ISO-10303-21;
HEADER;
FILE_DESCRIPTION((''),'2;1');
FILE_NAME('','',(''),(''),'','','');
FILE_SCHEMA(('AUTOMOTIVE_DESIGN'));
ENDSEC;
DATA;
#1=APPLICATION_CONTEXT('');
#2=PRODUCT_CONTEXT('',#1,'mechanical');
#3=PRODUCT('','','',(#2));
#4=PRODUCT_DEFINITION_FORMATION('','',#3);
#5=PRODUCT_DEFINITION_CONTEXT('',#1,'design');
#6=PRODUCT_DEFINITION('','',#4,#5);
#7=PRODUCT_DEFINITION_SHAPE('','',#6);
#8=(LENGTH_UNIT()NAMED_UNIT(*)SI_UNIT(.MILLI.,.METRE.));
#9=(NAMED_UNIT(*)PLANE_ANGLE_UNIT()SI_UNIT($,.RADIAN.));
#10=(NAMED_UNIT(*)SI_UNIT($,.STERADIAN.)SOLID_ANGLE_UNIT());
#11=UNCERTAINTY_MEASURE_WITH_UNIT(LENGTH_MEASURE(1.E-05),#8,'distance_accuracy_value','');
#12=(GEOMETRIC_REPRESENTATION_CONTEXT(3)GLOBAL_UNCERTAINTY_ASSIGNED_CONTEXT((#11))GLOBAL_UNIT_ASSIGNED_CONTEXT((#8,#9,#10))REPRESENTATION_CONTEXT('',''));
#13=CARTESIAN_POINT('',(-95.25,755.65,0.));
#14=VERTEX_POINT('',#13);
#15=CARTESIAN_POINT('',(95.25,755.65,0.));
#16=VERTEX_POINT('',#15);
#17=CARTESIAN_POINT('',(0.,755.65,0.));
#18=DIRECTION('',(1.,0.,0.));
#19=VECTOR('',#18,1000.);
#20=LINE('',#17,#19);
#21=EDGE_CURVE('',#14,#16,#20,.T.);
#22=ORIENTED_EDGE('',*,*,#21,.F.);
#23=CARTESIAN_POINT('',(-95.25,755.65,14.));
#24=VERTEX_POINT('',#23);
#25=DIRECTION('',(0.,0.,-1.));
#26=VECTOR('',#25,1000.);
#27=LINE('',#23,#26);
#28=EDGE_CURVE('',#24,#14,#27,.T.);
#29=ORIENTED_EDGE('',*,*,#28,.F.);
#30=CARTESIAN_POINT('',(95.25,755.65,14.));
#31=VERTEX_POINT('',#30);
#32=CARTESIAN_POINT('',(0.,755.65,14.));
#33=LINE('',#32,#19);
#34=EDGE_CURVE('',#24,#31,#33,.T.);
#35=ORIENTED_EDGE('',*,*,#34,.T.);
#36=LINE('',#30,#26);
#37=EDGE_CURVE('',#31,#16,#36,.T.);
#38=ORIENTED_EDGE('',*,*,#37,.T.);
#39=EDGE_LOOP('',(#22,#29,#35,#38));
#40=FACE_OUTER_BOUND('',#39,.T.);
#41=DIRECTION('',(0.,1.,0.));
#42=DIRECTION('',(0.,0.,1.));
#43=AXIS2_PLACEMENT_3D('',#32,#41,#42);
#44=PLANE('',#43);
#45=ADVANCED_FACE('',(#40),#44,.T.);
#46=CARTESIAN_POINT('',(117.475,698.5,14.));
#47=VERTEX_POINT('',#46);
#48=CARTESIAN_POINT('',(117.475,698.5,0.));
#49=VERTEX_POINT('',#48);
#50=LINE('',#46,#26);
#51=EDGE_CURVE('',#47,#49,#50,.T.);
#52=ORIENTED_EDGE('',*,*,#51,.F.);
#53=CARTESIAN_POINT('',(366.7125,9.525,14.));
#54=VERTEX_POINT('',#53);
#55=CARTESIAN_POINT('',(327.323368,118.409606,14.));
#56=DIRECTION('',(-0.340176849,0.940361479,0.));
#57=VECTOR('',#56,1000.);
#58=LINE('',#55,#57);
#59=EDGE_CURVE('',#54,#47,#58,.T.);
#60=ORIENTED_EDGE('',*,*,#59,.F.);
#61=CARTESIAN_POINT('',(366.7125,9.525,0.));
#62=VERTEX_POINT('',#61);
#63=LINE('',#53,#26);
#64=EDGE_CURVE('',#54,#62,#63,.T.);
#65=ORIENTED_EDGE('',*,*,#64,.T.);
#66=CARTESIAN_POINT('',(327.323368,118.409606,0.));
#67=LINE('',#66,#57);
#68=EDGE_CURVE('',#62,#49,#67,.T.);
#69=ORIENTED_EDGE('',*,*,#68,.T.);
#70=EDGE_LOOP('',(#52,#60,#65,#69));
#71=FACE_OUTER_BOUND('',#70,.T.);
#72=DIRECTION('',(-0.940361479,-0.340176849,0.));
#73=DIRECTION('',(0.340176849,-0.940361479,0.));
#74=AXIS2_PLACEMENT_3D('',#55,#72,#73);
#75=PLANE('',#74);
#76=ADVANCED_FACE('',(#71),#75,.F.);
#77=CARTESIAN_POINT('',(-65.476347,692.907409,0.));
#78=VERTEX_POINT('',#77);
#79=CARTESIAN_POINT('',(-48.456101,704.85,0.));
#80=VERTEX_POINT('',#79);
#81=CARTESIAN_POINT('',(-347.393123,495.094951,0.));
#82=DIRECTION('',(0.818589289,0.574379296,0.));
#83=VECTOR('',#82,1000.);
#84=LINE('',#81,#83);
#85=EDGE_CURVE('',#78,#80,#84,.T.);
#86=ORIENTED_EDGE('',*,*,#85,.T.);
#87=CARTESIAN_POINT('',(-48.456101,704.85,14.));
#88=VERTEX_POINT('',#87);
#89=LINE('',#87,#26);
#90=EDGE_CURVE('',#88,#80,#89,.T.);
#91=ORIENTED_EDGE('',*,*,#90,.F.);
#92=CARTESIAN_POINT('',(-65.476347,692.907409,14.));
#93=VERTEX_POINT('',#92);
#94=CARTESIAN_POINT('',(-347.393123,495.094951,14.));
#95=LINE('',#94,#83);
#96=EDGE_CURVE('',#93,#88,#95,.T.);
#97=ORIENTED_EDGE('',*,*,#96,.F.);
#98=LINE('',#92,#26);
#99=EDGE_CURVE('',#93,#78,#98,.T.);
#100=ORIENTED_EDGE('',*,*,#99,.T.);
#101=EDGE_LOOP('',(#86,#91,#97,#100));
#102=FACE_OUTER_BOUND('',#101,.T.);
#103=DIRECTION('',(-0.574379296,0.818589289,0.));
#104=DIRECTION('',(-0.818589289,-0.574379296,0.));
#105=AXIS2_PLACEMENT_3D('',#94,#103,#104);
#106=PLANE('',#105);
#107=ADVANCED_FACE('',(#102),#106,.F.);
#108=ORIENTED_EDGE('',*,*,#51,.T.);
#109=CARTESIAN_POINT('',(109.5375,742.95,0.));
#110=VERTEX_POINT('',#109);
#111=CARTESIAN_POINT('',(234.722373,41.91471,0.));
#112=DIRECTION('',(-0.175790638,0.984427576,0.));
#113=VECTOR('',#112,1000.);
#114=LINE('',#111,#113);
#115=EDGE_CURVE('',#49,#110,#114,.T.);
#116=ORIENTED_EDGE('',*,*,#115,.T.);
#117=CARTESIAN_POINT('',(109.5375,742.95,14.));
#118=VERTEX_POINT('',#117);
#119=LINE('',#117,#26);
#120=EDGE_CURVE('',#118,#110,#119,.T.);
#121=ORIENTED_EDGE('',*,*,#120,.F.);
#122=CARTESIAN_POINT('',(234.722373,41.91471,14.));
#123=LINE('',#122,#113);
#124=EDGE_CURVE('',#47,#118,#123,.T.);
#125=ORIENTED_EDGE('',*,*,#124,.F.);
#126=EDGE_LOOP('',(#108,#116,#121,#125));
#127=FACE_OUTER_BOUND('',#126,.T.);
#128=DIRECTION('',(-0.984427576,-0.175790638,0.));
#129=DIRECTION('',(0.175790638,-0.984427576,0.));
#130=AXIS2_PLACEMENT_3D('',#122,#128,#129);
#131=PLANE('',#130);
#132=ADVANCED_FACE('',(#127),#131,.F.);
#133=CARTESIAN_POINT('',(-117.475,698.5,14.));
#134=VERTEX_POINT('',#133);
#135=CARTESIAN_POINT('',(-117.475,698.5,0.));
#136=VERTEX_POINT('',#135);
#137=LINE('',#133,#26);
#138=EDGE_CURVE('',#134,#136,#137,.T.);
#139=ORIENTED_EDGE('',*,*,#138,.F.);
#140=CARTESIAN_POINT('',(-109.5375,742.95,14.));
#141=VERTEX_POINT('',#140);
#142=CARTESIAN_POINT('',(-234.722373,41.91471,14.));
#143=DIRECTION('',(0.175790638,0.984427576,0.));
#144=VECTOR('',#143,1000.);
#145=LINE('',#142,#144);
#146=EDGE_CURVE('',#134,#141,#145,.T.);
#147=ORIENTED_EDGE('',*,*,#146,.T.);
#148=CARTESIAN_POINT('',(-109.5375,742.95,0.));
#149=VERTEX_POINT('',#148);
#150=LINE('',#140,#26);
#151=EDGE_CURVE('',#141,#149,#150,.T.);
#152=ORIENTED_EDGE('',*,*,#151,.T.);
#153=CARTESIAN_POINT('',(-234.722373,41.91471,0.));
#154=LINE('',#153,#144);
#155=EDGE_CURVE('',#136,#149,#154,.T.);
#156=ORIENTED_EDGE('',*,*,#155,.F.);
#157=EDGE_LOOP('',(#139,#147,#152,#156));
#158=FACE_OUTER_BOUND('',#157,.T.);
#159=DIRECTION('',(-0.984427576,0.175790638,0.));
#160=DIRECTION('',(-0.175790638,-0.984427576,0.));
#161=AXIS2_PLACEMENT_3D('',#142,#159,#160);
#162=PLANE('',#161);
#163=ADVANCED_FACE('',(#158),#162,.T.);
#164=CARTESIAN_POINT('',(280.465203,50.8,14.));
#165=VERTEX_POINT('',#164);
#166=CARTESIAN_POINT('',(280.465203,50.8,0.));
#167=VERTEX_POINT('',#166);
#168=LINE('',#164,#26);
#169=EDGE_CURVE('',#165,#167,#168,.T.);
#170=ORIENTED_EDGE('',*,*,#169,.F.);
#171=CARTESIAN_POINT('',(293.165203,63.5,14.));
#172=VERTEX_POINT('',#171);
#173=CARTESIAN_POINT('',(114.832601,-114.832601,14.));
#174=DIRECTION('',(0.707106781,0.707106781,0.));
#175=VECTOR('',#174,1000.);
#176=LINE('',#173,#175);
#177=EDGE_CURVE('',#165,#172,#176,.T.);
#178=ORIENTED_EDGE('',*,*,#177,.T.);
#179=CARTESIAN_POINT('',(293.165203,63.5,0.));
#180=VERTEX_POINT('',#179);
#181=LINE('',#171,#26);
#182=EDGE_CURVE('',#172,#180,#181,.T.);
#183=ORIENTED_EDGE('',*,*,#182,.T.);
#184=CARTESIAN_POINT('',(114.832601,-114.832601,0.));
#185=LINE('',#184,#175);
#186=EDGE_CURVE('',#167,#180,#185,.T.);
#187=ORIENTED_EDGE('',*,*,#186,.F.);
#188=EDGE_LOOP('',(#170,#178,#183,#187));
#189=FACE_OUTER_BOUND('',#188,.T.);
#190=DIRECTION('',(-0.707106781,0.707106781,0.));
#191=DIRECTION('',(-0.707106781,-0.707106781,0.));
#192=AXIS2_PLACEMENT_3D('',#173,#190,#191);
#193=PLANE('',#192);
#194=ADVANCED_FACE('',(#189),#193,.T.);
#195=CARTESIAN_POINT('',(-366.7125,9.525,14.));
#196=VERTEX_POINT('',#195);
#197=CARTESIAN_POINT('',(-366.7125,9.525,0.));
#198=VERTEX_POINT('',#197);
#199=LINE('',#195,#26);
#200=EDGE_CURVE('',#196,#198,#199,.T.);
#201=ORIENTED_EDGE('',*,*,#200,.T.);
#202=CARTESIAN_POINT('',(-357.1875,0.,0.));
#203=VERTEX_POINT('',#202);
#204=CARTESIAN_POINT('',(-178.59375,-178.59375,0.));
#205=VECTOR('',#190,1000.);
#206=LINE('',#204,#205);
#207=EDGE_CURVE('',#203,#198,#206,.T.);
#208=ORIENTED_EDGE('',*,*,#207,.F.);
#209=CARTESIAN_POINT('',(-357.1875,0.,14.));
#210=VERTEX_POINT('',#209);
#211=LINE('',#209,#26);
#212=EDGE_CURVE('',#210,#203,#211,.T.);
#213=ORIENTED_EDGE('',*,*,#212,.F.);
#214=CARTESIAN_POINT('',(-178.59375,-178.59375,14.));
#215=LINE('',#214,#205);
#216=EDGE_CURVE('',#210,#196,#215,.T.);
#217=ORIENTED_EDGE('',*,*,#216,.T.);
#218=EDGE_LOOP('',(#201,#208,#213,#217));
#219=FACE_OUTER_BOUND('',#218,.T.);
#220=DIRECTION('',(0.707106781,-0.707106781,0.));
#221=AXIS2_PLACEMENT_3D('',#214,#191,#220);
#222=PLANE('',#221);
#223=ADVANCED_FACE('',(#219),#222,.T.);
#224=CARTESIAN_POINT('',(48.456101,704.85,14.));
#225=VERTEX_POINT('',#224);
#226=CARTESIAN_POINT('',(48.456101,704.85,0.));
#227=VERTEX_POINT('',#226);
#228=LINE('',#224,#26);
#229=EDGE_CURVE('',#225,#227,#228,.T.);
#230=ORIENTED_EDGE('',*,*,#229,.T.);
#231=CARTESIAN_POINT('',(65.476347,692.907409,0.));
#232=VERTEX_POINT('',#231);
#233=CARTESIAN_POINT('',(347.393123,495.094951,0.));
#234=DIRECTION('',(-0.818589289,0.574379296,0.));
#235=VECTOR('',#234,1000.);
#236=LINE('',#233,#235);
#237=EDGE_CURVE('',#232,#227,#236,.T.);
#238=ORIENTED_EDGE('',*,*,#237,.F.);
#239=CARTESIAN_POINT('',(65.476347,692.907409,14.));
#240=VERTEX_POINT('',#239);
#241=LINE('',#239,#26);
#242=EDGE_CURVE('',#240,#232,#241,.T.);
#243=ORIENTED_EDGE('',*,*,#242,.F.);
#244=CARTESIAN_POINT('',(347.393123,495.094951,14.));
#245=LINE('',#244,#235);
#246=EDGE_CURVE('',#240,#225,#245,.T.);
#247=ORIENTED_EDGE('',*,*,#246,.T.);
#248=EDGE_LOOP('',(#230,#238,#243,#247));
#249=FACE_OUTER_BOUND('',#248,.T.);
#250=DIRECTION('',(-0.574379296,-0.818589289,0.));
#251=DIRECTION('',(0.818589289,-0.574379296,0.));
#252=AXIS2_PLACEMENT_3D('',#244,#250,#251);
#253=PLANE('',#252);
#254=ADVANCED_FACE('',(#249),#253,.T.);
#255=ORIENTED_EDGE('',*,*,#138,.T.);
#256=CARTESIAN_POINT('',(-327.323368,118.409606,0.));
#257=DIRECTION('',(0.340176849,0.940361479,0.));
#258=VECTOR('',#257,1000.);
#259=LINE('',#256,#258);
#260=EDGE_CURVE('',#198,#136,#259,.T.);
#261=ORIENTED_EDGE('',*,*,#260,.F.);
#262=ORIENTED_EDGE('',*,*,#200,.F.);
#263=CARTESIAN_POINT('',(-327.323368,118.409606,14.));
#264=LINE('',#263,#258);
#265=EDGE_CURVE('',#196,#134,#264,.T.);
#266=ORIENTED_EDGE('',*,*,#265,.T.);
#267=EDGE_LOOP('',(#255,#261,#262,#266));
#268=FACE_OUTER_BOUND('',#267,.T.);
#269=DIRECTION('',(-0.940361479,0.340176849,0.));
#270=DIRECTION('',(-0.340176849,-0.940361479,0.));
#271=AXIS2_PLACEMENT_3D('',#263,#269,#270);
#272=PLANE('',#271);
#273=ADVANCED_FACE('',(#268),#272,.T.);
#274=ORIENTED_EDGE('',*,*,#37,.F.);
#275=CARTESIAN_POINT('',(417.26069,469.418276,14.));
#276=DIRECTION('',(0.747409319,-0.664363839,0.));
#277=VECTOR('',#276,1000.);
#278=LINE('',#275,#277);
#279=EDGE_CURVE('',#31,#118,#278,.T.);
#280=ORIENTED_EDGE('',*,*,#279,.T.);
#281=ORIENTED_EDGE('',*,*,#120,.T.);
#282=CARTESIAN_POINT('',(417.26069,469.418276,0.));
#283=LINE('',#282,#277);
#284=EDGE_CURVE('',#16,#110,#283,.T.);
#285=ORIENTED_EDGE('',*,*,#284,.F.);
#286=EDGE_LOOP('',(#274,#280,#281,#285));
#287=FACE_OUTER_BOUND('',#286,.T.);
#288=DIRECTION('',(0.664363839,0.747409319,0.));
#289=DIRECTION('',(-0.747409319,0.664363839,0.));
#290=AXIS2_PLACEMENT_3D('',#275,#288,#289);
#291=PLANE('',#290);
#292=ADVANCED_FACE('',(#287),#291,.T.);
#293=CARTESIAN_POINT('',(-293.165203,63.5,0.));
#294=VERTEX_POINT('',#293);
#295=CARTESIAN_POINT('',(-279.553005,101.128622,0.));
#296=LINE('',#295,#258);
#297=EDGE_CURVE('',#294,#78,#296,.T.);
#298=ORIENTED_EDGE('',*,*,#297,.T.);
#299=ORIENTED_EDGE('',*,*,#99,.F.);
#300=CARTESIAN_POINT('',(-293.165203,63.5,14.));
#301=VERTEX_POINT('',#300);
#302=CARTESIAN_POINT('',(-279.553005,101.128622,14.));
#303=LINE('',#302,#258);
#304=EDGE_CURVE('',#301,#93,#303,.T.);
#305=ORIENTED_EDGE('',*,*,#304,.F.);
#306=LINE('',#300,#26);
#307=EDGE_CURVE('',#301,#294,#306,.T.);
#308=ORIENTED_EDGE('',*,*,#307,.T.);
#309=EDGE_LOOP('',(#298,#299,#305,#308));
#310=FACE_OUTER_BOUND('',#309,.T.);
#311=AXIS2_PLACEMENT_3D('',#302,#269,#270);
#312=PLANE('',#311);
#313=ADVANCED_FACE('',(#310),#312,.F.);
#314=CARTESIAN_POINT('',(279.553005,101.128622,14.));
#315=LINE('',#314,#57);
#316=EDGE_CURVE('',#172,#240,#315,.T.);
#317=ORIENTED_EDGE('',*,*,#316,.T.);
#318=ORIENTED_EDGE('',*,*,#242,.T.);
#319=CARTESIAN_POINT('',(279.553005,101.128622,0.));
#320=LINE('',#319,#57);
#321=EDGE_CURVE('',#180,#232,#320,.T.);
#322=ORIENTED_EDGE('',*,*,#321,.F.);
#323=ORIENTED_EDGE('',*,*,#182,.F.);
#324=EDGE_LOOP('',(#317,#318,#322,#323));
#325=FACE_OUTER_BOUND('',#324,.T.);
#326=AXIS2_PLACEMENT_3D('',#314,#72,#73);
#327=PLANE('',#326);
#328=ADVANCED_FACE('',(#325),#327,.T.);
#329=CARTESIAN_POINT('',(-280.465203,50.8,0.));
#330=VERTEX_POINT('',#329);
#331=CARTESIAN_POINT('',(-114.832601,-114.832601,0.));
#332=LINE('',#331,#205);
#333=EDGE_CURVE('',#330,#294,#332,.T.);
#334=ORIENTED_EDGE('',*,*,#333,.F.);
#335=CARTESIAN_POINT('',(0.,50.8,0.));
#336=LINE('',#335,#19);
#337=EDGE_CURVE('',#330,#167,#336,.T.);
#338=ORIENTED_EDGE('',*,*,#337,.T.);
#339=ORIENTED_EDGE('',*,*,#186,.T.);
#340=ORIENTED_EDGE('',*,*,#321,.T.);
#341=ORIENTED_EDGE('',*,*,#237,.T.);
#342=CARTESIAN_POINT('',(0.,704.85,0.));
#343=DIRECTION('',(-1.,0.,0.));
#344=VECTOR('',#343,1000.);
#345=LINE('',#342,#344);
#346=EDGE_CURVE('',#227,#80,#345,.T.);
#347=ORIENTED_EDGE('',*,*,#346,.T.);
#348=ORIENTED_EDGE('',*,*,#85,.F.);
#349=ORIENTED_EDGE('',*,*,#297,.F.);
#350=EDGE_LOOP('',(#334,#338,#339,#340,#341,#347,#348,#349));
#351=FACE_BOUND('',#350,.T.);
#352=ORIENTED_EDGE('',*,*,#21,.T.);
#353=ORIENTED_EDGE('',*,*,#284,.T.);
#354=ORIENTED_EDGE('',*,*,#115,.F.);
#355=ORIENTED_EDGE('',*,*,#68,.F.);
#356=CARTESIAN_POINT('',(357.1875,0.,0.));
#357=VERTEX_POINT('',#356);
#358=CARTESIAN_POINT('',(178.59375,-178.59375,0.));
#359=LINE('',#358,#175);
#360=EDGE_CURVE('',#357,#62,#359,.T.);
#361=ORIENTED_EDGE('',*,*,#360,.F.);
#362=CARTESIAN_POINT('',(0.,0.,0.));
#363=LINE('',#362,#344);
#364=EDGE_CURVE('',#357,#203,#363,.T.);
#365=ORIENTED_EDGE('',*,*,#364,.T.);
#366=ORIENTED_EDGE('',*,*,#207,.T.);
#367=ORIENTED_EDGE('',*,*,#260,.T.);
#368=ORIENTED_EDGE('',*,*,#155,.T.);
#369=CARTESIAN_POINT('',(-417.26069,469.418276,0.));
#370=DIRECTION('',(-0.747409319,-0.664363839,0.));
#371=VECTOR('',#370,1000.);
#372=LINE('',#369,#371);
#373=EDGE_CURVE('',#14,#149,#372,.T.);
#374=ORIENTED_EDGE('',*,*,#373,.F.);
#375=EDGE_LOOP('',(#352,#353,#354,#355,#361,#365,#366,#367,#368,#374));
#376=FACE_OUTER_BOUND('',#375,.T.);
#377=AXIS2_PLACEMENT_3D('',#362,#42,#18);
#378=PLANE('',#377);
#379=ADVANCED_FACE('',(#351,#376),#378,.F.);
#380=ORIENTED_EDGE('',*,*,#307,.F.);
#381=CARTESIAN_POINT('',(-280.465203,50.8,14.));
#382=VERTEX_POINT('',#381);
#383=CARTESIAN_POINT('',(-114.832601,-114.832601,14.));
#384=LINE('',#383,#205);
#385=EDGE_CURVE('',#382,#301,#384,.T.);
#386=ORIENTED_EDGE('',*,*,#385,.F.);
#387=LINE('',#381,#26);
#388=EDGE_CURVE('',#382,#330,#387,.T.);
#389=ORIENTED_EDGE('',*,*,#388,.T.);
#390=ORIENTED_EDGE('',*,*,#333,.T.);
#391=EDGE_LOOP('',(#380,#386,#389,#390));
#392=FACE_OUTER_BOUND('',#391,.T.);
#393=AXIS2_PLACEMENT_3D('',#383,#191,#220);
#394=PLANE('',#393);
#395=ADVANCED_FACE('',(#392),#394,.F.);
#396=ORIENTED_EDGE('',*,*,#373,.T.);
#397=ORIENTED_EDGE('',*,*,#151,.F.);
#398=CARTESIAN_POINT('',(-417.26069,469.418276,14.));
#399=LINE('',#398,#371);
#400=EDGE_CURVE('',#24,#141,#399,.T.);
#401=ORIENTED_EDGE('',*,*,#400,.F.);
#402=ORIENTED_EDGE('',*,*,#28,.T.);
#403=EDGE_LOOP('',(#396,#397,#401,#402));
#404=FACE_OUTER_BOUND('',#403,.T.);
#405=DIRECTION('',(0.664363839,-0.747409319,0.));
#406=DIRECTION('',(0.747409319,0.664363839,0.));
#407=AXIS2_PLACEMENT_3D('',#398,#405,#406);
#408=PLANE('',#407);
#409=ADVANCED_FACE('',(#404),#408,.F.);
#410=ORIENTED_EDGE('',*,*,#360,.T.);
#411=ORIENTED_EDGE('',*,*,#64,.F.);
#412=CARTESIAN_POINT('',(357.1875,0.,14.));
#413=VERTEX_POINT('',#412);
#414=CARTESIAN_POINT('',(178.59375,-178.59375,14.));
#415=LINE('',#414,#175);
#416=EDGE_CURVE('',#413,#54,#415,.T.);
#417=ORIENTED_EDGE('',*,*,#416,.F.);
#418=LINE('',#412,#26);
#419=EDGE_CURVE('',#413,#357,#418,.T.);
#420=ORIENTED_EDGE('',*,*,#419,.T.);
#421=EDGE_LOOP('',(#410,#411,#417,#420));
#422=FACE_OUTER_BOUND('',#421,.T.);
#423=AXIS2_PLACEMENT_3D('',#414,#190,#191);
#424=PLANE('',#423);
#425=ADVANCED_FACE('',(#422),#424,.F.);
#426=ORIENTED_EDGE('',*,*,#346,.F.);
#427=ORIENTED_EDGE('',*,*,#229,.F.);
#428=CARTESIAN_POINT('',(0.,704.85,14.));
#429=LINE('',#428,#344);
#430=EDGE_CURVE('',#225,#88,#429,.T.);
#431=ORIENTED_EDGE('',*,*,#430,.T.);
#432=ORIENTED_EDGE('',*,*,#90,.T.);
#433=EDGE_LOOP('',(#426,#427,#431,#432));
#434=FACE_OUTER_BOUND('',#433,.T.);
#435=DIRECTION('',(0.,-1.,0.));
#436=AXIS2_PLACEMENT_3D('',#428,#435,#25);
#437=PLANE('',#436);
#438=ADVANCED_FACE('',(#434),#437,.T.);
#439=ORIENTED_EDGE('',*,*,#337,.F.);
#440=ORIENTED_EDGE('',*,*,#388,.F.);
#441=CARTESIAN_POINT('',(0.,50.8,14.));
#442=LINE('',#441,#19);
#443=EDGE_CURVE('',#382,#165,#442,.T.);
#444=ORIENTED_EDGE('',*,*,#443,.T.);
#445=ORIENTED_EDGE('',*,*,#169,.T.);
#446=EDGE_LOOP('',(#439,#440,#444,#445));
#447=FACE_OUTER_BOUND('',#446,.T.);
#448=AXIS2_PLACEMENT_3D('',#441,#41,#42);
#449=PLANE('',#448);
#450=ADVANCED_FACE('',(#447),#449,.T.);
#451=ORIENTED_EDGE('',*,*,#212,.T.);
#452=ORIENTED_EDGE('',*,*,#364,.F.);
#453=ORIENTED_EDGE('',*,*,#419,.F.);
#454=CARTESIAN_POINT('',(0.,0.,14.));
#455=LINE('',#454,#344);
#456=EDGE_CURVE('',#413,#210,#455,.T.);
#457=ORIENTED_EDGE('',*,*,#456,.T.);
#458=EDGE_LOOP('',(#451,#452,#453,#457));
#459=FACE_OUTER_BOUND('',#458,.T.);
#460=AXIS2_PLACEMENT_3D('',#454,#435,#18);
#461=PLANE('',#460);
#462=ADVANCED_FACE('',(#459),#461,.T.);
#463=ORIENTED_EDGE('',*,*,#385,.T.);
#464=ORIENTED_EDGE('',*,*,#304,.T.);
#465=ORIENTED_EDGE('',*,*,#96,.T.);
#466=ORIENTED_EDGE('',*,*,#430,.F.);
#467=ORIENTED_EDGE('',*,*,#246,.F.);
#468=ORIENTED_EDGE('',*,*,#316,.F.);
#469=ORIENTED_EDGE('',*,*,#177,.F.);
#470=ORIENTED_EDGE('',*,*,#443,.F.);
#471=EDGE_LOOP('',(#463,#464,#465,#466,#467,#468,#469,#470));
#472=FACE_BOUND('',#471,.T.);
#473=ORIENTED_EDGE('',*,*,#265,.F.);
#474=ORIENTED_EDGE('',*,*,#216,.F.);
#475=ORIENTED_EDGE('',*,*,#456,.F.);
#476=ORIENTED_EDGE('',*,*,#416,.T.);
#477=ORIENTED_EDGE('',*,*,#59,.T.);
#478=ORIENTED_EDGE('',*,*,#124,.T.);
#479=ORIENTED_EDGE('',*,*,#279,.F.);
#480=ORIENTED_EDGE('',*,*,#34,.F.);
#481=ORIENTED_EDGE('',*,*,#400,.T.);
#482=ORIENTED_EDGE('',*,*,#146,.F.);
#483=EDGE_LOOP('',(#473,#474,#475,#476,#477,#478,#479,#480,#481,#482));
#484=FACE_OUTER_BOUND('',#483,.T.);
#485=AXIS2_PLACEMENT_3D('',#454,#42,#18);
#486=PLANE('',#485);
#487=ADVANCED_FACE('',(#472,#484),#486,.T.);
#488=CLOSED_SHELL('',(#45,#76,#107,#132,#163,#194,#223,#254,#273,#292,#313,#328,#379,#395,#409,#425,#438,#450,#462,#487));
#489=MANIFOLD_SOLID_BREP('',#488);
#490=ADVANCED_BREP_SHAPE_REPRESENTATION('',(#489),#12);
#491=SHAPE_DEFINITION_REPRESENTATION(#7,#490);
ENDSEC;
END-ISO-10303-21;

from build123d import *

# Parameters (mm, degrees)
BOSS_EXTRUDE1_DEPTH = 14


with BuildPart() as part:
    # Sketch1 → Boss-Extrude1 (new body)
    with BuildSketch(Plane.XY):
        Polygon((-95.25, 755.65), (0, 755.65), (95.25, 755.65), (109.5375, 742.95), (117.475, 698.5), (366.7125, 9.525), (357.1875, 0), (0, 0), (-357.1875, 0), (-366.7125, 9.525), (-117.475, 698.5), (-109.5375, 742.95), align=None)
        Polygon((-280.465202582, 50.8), (280.465202582, 50.8), (293.165202582, 63.5), (65.476347176, 692.907409213), (48.4561012, 704.85), (-48.4561012, 704.85), (-65.476347176, 692.907409213), (-293.165202582, 63.5), align=None, mode=Mode.SUBTRACT)
    extrude(amount=BOSS_EXTRUDE1_DEPTH)


solid = part.part
